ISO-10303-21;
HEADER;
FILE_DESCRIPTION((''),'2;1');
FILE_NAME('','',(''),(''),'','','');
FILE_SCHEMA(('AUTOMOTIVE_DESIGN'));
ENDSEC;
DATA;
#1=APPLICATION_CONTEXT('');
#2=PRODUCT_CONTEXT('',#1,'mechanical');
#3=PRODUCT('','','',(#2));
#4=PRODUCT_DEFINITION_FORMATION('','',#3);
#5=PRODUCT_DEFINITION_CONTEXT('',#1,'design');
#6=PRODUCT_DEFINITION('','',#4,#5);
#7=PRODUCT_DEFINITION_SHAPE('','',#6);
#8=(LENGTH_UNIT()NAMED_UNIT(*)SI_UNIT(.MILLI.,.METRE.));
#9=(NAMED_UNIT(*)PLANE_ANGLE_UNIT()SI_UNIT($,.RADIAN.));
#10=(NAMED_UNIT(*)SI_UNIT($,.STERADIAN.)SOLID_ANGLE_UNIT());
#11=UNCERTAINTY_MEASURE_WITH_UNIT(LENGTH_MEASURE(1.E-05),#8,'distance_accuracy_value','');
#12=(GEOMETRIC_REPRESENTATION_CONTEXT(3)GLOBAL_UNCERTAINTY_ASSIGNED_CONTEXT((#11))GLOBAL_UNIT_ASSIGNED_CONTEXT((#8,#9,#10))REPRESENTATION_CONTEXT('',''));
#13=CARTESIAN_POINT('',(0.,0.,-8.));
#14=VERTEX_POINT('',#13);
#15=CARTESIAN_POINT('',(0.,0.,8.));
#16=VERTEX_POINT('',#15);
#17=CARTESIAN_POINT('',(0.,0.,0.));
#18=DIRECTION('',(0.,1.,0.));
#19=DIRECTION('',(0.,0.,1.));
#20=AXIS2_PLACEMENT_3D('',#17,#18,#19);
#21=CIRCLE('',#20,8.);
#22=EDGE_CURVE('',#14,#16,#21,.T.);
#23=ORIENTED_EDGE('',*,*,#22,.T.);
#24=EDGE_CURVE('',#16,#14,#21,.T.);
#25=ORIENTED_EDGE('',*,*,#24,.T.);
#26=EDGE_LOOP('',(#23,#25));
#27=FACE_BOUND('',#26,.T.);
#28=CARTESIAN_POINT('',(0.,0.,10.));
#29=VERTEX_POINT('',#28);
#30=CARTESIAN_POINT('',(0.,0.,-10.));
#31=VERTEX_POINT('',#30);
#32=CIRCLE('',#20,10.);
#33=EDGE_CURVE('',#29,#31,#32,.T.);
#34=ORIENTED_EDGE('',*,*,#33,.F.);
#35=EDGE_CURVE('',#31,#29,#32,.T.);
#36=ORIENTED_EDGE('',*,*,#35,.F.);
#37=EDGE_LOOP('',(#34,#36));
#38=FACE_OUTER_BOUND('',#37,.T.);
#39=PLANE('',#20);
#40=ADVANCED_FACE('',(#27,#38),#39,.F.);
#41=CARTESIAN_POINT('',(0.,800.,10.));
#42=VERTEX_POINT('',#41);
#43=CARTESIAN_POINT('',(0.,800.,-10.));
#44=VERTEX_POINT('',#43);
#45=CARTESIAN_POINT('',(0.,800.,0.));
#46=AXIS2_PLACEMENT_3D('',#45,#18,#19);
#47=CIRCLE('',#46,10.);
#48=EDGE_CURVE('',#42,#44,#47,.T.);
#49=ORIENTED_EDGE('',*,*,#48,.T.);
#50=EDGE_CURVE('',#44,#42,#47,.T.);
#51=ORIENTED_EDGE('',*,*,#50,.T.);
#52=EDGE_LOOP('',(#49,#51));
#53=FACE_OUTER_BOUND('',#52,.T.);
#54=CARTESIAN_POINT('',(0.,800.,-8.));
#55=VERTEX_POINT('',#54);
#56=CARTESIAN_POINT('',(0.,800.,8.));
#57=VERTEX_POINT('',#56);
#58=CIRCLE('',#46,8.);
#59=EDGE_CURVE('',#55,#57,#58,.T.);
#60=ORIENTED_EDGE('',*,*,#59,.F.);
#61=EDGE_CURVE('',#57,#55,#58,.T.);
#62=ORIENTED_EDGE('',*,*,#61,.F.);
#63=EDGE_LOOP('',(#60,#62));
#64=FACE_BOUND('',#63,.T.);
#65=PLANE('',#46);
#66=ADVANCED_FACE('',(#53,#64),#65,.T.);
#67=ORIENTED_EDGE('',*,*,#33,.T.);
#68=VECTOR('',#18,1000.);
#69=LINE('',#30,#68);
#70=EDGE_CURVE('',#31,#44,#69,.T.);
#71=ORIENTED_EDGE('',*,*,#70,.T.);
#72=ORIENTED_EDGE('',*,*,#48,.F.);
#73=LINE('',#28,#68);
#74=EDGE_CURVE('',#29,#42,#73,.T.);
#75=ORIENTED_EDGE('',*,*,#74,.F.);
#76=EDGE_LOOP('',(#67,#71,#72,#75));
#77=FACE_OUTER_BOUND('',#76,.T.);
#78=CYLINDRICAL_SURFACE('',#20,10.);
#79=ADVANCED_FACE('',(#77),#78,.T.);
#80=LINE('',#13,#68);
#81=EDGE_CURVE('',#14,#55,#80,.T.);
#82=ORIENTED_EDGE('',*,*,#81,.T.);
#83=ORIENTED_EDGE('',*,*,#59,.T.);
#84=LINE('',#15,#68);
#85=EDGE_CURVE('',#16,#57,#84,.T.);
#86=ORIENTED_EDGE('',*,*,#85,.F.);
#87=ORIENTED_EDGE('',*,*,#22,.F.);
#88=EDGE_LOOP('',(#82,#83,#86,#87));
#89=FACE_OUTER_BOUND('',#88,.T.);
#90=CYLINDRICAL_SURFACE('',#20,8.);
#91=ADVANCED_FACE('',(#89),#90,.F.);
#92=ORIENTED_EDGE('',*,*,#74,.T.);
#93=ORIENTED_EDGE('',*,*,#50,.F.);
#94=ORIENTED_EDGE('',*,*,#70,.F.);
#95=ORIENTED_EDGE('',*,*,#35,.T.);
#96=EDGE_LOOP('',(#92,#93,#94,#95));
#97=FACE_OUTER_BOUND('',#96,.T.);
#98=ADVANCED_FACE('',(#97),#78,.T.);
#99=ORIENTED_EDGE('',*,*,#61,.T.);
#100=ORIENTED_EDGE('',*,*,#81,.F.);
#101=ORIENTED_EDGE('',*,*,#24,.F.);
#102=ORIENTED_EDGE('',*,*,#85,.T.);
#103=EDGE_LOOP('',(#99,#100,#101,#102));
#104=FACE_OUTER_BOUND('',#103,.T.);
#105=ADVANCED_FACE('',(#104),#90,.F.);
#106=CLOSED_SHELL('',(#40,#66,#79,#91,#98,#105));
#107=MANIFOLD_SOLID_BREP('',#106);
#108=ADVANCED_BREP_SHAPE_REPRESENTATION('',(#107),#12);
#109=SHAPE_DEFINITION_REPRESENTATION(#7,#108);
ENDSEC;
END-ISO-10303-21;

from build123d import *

# Parameters (mm, degrees)
SWEEP_THIN1_PROFILE_R   = 10
SWEEP_THIN1_PROFILE_R_2 = 8


with BuildPart() as part:
    # Sweep-Thin1: sweep along a path in Sketch1
    with BuildLine(Plane.XY) as sweep_thin1_path:
        Line((0, 0), (0, 800))
    # Sweep-Thin1 profile (on start of the path) → Sweep-Thin1 (sweep)
    with BuildSketch(Plane.ZX):
        Circle(SWEEP_THIN1_PROFILE_R)
        Circle(SWEEP_THIN1_PROFILE_R_2, mode=Mode.SUBTRACT)
    sweep(path=sweep_thin1_path.line)


solid = part.part
